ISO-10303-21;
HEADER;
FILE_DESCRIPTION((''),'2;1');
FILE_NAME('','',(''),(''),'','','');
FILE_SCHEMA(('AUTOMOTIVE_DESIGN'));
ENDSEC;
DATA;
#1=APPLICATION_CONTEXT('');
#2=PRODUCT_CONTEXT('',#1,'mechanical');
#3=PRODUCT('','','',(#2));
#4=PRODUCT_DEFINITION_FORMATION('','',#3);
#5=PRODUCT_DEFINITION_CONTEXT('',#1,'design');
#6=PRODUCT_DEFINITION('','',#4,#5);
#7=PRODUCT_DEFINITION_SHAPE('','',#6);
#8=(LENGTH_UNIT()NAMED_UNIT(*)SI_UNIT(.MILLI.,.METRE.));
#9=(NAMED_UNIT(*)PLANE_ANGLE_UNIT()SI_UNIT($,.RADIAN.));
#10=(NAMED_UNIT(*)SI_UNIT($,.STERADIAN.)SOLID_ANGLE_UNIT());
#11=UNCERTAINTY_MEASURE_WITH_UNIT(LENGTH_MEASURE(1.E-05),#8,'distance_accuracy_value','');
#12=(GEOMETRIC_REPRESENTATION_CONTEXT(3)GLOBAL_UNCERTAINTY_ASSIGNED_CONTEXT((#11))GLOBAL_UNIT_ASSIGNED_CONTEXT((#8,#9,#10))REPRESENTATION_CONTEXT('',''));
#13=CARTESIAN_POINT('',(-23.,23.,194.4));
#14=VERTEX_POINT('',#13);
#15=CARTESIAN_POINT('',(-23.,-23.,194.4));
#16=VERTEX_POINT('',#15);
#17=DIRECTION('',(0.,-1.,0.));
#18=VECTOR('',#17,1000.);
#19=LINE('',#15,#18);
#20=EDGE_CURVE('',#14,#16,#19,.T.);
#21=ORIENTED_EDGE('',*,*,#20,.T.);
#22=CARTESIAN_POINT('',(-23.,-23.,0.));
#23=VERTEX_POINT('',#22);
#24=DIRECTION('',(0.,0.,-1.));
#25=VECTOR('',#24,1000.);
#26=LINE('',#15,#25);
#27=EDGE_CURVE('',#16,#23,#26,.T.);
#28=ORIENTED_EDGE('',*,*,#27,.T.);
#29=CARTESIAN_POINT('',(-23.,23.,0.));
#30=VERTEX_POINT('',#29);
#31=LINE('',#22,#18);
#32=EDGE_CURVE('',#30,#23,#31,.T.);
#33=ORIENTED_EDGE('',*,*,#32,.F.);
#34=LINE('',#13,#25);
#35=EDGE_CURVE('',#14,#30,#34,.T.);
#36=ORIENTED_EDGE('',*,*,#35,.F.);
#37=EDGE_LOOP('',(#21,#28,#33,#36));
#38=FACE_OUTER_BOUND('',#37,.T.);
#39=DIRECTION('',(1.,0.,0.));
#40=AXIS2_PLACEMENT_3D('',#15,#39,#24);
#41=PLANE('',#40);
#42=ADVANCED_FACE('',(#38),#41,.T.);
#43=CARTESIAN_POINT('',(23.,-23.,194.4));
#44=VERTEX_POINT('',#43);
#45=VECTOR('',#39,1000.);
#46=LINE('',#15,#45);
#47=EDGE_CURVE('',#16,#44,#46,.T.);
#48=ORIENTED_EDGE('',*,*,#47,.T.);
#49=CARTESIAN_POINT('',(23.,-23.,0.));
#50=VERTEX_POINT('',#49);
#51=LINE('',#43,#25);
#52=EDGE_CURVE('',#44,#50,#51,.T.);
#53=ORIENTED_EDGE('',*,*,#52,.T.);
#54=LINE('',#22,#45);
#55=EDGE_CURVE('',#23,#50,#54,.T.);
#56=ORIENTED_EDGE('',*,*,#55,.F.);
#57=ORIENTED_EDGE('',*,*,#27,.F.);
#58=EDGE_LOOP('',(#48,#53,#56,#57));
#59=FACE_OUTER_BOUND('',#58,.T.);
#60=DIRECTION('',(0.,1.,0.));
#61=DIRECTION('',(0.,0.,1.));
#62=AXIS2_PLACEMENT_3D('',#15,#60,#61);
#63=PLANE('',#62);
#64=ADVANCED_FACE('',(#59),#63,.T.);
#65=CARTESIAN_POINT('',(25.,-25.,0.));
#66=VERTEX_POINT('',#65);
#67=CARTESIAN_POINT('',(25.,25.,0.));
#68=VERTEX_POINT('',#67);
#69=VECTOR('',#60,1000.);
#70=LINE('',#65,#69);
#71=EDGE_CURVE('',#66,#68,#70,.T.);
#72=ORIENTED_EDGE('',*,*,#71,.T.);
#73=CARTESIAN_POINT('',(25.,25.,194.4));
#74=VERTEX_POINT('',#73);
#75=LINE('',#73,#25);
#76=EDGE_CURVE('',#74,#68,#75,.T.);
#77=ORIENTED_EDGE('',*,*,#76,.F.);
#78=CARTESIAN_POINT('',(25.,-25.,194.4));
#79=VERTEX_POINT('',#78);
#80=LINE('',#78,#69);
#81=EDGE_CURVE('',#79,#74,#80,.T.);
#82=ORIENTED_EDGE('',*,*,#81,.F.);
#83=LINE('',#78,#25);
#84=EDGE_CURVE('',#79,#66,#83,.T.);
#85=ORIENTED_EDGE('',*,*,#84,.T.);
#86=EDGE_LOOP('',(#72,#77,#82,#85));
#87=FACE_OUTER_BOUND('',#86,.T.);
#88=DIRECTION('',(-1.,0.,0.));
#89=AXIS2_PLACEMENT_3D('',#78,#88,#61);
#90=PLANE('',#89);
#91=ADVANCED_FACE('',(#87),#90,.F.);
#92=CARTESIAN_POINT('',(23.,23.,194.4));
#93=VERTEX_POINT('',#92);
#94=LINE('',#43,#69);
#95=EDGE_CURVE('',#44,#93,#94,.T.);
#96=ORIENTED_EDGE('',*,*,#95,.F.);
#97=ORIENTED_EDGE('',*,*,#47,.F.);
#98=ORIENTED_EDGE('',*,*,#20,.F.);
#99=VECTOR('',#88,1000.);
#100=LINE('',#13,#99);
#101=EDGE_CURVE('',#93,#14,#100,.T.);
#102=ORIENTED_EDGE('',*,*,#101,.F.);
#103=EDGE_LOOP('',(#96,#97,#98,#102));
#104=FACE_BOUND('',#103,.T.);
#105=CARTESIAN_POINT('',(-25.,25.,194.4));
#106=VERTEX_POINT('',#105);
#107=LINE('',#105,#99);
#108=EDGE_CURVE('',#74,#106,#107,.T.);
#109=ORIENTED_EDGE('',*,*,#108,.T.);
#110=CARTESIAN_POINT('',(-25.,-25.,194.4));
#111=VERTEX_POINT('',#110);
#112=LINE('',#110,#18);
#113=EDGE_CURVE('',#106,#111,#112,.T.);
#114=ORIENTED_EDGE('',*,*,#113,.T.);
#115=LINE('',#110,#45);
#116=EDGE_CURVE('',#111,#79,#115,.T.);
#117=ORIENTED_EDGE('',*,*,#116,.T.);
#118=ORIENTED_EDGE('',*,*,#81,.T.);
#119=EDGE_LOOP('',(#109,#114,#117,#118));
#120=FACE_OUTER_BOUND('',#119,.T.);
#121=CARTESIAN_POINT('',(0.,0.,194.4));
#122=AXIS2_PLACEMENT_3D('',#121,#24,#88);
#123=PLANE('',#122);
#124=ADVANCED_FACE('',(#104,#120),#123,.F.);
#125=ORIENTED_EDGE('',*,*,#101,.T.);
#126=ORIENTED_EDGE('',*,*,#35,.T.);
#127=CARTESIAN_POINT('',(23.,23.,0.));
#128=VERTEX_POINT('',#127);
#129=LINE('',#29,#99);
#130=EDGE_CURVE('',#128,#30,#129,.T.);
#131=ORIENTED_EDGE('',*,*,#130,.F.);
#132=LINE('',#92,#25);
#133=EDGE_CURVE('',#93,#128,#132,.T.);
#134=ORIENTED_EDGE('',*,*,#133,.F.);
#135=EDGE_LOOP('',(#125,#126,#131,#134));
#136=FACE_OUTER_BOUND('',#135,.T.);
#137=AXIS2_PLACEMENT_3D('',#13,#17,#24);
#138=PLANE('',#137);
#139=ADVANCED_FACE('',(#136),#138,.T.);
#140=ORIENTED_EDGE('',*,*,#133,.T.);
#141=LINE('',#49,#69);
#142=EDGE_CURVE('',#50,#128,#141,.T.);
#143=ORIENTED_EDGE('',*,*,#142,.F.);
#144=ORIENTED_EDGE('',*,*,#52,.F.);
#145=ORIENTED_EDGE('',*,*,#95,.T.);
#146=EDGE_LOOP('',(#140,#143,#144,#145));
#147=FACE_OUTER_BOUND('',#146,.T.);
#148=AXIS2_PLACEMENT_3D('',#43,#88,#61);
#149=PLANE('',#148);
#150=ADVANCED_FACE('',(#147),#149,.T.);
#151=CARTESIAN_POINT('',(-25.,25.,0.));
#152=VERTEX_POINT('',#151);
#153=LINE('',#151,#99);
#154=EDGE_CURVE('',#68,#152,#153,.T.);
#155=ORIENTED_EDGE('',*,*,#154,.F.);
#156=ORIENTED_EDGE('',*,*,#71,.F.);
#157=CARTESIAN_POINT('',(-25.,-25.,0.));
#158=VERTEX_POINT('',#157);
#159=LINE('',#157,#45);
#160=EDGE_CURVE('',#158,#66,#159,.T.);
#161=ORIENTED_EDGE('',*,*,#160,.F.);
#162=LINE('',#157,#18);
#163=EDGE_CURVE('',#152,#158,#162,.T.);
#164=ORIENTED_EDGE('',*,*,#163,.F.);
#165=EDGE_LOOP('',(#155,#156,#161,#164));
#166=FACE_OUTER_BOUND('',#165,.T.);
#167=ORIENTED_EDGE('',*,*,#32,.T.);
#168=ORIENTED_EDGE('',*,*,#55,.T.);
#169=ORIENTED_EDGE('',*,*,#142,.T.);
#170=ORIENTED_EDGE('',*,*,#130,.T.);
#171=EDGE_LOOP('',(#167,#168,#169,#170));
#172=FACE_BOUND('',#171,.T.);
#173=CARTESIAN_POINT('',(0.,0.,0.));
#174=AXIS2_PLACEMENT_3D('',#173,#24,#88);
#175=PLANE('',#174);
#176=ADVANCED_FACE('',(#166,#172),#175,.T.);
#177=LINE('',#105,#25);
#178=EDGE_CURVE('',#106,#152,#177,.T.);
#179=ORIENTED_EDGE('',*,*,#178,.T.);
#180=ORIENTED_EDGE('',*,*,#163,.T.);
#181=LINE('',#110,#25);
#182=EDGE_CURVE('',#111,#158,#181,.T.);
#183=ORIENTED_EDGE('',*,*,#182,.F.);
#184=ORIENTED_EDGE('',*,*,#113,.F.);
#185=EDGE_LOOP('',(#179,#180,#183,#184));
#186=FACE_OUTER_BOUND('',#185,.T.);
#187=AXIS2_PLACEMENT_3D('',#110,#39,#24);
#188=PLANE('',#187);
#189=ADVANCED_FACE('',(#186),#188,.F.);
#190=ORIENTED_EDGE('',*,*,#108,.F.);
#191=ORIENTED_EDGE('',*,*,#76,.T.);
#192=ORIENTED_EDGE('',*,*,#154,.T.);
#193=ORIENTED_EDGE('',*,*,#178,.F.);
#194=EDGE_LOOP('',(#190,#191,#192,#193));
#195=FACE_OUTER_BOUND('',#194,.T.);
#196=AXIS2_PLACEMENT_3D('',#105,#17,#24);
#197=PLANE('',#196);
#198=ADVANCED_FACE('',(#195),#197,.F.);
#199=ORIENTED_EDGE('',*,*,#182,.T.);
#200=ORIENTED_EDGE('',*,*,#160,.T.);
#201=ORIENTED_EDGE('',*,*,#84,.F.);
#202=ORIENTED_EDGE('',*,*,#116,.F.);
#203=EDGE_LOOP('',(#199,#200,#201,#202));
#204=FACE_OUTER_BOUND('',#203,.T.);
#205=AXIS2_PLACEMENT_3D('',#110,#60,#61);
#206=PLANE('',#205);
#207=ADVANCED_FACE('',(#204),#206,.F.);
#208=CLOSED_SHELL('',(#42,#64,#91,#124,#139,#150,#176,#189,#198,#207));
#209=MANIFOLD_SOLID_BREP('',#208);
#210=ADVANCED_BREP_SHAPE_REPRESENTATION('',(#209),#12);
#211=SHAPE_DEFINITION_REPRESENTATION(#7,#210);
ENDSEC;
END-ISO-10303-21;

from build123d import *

# Parameters (mm, degrees)
SKETCH1_W           = 50
SKETCH1_H           = 50
SKETCH1_W_2         = 46
SKETCH1_H_2         = 46
BOSS_EXTRUDE1_DEPTH = 194.4


with BuildPart() as part:
    # Sketch1 → Boss-Extrude1 (new body)
    with BuildSketch(Plane.XY):
        Rectangle(SKETCH1_W, SKETCH1_H)
        Rectangle(SKETCH1_W_2, SKETCH1_H_2, mode=Mode.SUBTRACT)
    extrude(amount=BOSS_EXTRUDE1_DEPTH)


solid = part.part
